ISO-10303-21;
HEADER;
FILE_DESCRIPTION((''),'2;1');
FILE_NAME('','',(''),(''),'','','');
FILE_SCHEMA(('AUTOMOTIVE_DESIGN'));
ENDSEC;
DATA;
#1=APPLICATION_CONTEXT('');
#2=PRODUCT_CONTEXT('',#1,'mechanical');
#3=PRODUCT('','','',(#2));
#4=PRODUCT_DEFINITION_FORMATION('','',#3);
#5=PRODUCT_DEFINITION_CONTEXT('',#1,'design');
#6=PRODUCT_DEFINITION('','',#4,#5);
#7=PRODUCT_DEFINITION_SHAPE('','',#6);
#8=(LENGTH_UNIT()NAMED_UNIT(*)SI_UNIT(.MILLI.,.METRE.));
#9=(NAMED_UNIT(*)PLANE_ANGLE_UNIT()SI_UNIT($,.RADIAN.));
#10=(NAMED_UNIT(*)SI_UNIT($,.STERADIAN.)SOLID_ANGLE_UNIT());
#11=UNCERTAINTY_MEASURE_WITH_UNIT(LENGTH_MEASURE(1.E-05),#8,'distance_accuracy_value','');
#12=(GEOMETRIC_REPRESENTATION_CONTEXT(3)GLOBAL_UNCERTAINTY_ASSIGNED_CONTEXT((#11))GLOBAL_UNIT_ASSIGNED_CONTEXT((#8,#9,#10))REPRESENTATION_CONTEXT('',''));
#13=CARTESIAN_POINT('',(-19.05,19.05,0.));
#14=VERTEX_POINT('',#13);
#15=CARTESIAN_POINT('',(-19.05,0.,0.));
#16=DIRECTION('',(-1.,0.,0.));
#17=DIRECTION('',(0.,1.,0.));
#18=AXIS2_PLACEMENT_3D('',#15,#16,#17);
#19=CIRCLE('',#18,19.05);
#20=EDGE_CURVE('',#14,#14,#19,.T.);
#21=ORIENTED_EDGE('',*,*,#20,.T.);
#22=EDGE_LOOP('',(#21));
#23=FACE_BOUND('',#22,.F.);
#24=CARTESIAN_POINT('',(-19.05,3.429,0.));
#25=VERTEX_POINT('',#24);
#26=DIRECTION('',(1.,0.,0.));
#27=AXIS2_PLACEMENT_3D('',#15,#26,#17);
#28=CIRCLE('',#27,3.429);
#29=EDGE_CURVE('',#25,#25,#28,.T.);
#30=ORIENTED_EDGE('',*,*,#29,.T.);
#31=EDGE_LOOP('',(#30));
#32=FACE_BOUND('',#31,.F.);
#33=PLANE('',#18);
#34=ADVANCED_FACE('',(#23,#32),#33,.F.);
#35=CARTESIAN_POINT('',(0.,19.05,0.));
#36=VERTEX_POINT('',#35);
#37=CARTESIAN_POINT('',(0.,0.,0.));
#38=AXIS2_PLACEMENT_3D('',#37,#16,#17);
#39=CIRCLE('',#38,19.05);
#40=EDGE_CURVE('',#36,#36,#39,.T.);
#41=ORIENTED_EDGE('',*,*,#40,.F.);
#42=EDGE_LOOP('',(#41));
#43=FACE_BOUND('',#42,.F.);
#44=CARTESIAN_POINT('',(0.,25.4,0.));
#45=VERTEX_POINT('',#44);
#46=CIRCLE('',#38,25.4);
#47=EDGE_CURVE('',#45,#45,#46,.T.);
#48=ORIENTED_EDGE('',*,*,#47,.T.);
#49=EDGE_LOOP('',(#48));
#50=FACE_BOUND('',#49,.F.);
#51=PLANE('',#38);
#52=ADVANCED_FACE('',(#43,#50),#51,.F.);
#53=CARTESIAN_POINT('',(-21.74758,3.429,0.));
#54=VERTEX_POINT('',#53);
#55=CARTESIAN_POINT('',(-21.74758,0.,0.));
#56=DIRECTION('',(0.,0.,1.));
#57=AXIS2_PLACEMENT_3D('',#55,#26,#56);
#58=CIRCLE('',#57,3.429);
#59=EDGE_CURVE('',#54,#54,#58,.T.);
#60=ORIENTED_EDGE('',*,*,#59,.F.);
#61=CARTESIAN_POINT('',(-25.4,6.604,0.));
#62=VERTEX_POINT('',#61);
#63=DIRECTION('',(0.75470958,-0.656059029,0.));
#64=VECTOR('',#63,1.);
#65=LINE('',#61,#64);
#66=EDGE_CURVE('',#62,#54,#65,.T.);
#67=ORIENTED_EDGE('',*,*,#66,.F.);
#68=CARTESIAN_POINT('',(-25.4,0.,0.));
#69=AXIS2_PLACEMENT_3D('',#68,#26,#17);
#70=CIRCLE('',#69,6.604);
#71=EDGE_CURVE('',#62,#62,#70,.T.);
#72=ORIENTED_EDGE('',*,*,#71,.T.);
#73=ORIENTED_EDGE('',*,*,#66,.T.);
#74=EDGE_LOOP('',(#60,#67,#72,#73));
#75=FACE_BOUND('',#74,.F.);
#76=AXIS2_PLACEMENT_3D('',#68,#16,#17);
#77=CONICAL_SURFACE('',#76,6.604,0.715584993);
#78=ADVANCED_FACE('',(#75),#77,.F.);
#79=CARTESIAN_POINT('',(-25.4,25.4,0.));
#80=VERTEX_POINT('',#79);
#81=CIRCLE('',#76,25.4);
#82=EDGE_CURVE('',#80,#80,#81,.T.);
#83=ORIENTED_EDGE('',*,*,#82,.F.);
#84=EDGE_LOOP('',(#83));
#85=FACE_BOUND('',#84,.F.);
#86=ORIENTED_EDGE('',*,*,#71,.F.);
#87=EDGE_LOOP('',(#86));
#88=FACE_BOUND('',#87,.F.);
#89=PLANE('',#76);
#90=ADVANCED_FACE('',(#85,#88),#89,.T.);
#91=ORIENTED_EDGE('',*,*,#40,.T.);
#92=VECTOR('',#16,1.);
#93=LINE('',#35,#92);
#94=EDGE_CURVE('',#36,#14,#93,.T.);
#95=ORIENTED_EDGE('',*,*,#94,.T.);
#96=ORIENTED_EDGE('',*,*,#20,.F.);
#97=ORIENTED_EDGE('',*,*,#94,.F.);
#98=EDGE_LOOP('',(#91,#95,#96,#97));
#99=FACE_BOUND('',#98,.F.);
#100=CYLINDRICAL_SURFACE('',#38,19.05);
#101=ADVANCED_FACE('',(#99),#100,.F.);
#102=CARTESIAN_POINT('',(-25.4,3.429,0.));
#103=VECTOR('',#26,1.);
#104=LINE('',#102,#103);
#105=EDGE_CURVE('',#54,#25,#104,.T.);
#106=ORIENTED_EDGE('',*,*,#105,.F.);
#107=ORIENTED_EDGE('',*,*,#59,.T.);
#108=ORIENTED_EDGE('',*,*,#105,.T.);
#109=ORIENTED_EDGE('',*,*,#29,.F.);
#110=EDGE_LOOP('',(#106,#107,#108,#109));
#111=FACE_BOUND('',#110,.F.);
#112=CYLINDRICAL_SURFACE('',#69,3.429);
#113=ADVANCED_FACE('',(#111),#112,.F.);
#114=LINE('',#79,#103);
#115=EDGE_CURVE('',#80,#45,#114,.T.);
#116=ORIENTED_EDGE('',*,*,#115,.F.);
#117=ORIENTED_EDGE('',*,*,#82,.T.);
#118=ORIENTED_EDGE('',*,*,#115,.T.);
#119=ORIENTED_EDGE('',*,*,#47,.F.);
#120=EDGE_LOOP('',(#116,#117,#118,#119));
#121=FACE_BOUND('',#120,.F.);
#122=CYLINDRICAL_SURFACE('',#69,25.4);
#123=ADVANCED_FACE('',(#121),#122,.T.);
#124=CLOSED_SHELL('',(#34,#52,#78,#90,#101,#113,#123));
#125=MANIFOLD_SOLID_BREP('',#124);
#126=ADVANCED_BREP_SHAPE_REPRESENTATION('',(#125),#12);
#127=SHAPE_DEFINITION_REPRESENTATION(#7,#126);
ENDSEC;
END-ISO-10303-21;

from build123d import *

# Parameters (mm, degrees)
COUNTERSUNK_CENTRE_HOLE_D                     = 6.858
COUNTERSUNK_CENTRE_HOLE_DEPTH                 = 19.05
COUNTERSUNK_CENTRE_HOLE_CSINK_D               = 13.208
COUNTERSUNK_CENTRE_HOLE_CSINK_ANGLE           = 82
COUNTERSUNK_CENTRE_HOLE_TIP                   = 2.060351063
COUNTERSUNK_CENTRE_HOLE_ON_FACE_2_D           = 6.858
COUNTERSUNK_CENTRE_HOLE_ON_FACE_2_DEPTH       = 19.05
COUNTERSUNK_CENTRE_HOLE_ON_FACE_2_CSINK_D     = 13.208
COUNTERSUNK_CENTRE_HOLE_ON_FACE_2_CSINK_ANGLE = 82
COUNTERSUNK_CENTRE_HOLE_ON_FACE_2_TIP         = 2.060351063


with BuildPart() as part:
    # Cup Profile Sketch → Cup Body Revolve (revolve)
    with BuildSketch(Plane.XY):
        Polygon((-19.05, 0), (-25.4, 0), (-25.4, 25.4), (0, 25.4), (0, 19.05), (-19.05, 19.05), align=None)
    revolve(axis=Axis((-19.05, 0, 0), (-1, 0, 0)))

    # Countersunk Centre Hole
    with Locations(Plane(origin=(-25.4, 0, 0), x_dir=(0, -1, 0), z_dir=(-1, 0, 0))):
        with Locations((0, 0)):
            CounterSinkHole(COUNTERSUNK_CENTRE_HOLE_D / 2, COUNTERSUNK_CENTRE_HOLE_CSINK_D / 2, depth=COUNTERSUNK_CENTRE_HOLE_DEPTH, counter_sink_angle=COUNTERSUNK_CENTRE_HOLE_CSINK_ANGLE)
            with Locations((0, 0, -(COUNTERSUNK_CENTRE_HOLE_DEPTH + COUNTERSUNK_CENTRE_HOLE_TIP / 2))):  # 118° drill point
                Cone(0, COUNTERSUNK_CENTRE_HOLE_D / 2, COUNTERSUNK_CENTRE_HOLE_TIP, mode=Mode.SUBTRACT)

    # Countersunk Centre Hole on face 2
    with Locations(Plane(origin=(0, 0, 0), x_dir=(0, -1, 0), z_dir=(-1, 0, 0))):
        with Locations((0, 0)):
            CounterSinkHole(COUNTERSUNK_CENTRE_HOLE_ON_FACE_2_D / 2, COUNTERSUNK_CENTRE_HOLE_ON_FACE_2_CSINK_D / 2, depth=COUNTERSUNK_CENTRE_HOLE_ON_FACE_2_DEPTH, counter_sink_angle=COUNTERSUNK_CENTRE_HOLE_ON_FACE_2_CSINK_ANGLE)
            with Locations((0, 0, -(COUNTERSUNK_CENTRE_HOLE_ON_FACE_2_DEPTH + COUNTERSUNK_CENTRE_HOLE_ON_FACE_2_TIP / 2))):  # 118° drill point
                Cone(0, COUNTERSUNK_CENTRE_HOLE_ON_FACE_2_D / 2, COUNTERSUNK_CENTRE_HOLE_ON_FACE_2_TIP, mode=Mode.SUBTRACT)


solid = part.part
